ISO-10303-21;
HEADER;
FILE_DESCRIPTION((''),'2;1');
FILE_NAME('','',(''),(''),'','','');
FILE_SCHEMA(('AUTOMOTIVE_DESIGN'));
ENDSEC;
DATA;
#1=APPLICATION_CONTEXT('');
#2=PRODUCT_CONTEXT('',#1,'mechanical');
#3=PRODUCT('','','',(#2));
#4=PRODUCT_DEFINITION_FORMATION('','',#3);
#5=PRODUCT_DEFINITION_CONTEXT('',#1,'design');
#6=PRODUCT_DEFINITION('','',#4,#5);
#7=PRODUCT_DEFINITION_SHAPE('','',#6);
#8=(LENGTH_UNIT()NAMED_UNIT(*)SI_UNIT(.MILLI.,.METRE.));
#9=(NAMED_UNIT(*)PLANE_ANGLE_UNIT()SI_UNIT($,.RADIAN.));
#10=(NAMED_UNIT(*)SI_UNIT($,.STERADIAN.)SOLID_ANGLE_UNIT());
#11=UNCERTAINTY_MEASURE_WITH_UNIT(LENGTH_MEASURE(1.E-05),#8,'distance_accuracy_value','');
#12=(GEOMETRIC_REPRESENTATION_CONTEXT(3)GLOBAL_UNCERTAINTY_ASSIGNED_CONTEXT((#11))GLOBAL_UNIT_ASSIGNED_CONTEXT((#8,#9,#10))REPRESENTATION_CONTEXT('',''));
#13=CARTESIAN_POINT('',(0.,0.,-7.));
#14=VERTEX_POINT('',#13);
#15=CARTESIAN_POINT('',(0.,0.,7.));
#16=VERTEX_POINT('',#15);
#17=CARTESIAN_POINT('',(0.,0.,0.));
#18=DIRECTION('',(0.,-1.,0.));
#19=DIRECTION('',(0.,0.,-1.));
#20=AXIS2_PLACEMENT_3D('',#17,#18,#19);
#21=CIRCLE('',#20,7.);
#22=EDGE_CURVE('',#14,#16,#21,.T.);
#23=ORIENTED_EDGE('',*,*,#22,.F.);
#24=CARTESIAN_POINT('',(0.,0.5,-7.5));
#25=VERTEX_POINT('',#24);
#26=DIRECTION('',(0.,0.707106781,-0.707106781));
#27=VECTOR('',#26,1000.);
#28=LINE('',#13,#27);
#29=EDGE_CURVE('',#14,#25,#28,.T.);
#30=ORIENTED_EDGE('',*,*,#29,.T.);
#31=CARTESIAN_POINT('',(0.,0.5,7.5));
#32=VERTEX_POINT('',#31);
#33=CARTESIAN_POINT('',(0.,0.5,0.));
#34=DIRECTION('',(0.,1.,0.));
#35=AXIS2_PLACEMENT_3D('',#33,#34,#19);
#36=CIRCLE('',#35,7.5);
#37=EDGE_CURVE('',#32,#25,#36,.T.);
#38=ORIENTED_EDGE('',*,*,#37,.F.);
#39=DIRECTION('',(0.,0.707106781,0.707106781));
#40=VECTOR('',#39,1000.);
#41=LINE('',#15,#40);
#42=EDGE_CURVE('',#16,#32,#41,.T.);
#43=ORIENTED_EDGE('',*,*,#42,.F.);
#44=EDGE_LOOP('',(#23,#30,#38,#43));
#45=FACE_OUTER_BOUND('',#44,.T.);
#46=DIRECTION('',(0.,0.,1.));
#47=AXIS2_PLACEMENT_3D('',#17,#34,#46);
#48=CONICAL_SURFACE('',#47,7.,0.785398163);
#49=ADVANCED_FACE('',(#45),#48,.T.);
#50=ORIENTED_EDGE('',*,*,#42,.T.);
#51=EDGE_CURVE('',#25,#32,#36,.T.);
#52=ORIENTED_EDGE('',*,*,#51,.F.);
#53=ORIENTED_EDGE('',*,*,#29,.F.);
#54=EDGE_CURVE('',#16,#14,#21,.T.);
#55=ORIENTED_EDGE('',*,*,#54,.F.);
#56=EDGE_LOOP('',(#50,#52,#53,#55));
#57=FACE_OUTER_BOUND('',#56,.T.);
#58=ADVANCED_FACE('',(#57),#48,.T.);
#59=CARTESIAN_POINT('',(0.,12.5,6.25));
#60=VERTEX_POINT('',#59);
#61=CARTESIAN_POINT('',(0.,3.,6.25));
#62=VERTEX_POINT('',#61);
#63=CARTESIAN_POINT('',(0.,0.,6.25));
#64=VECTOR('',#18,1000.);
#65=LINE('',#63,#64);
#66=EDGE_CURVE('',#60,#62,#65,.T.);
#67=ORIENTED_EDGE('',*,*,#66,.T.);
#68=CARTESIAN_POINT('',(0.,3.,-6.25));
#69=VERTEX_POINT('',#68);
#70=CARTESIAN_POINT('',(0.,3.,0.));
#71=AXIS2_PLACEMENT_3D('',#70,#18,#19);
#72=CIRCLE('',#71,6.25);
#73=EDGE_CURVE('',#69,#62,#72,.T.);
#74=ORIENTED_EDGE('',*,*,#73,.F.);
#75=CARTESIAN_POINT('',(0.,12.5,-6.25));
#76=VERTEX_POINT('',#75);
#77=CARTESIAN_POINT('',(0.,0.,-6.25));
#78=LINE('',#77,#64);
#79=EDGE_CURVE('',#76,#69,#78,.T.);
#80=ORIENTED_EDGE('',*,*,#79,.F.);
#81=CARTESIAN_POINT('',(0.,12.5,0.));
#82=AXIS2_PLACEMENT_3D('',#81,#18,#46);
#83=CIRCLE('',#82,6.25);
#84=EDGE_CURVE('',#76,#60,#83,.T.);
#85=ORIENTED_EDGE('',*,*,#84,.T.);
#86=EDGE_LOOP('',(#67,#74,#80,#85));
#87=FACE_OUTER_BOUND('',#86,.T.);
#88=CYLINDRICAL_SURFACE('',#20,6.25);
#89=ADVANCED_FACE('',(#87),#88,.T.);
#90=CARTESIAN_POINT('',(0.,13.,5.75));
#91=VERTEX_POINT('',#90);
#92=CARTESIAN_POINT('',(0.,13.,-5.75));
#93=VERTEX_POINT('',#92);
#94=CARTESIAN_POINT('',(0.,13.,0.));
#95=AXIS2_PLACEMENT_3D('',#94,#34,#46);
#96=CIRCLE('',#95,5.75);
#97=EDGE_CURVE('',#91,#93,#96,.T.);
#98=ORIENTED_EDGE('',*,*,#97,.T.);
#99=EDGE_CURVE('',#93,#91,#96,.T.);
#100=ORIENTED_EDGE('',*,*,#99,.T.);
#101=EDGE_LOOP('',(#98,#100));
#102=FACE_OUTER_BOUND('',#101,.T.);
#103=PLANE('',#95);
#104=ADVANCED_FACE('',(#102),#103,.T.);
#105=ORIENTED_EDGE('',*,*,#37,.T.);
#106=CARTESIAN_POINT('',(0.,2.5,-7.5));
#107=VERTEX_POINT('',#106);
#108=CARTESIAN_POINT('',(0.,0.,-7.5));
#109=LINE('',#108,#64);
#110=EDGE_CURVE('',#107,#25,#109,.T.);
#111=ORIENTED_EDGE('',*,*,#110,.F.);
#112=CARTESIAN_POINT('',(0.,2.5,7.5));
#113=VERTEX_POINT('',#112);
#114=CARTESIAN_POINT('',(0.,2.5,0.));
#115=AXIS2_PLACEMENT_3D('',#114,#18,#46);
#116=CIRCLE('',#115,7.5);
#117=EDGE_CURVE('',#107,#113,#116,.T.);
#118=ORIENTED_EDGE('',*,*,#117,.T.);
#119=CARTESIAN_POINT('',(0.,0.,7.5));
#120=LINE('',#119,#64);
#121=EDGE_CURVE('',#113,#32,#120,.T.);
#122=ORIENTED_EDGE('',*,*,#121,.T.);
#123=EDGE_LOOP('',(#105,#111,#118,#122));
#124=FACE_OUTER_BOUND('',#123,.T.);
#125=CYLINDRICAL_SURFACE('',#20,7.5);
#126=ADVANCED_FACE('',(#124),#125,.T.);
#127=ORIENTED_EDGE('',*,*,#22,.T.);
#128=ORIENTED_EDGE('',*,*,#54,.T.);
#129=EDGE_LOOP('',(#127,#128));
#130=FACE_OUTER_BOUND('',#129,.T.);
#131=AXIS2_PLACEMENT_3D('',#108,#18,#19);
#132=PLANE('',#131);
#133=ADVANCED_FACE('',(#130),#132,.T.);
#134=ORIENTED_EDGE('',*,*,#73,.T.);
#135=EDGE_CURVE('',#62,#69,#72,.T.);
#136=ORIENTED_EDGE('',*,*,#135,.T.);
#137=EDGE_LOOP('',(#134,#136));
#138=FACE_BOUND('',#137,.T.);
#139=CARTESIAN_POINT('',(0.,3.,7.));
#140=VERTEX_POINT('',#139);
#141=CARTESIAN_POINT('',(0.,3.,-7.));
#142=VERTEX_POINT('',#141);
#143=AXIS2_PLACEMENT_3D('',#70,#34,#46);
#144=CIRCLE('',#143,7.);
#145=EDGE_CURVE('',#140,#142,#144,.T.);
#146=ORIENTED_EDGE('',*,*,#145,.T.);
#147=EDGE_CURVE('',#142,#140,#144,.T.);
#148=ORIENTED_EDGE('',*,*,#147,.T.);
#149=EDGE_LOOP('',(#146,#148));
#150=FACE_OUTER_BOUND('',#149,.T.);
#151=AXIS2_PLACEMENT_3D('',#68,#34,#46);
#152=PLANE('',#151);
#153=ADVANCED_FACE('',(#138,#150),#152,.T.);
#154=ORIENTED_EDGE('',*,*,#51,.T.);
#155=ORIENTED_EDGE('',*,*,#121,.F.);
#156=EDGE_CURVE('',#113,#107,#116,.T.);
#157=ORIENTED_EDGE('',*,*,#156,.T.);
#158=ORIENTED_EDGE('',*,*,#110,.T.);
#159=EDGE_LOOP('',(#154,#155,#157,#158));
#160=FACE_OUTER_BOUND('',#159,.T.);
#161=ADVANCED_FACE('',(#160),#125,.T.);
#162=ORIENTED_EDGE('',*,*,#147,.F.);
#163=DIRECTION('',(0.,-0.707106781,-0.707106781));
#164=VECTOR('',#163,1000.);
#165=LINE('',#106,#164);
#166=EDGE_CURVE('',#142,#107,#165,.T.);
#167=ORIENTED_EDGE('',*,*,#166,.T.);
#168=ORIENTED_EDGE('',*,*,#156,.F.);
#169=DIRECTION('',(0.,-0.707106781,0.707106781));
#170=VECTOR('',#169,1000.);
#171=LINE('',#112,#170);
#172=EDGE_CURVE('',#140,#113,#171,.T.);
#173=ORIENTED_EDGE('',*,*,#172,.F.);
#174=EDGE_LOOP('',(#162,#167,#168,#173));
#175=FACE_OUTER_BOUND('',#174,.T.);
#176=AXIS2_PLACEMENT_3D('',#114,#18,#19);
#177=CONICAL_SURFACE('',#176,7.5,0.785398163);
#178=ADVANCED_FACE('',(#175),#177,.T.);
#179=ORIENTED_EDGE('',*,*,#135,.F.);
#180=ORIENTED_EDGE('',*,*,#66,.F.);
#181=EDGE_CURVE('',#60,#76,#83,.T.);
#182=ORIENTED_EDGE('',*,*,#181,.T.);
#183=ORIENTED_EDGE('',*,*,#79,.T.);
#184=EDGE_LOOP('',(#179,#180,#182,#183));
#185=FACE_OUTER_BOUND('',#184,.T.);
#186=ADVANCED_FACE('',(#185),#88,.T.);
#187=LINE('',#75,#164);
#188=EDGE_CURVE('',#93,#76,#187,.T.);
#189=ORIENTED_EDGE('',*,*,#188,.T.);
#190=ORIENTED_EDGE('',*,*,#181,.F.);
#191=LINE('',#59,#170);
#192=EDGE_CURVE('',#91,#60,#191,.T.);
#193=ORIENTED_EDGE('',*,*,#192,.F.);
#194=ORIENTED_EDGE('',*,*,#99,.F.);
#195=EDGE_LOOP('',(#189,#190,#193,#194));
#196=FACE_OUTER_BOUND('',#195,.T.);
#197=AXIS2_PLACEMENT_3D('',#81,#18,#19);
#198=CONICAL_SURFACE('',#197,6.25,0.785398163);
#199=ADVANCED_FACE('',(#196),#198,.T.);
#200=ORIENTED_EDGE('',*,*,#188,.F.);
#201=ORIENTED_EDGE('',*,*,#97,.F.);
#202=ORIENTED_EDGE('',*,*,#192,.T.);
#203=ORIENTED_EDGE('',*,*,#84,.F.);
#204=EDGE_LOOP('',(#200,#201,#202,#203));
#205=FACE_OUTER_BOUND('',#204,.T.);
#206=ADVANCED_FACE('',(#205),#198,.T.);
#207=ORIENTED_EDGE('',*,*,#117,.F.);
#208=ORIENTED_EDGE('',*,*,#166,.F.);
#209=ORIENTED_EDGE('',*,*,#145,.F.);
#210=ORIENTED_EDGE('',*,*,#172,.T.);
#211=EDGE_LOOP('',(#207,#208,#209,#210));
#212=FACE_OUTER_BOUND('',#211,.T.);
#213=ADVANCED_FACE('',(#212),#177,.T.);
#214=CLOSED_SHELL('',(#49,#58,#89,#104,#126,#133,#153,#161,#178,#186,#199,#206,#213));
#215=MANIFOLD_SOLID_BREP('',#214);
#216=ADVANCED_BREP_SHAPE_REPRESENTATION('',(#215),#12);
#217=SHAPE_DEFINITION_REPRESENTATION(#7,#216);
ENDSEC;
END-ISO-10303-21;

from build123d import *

# Parameters (mm, degrees)
CHAMFER1_SIZE = 0.5


with BuildPart() as part:
    # Sketch1 → Revolve1 (revolve)
    with BuildSketch(Plane(origin=(0, 0, 0), x_dir=(0, 0, -1), z_dir=(1, 0, 0))):
        Polygon((0, 13), (6.25, 13), (6.25, 3), (7.5, 3), (7.5, 0), (0, 0), align=None)
    revolve(axis=Axis((0, 0, 0), (0, 1, 0)))

    # Chamfer1
    chamfer1_edges = [part.edges().sort_by_distance(p)[0] for p in [
        (0, 0, 7.5),
        (0, 3, 7.5),
        (0, 13, 6.25),
    ]]
    chamfer(chamfer1_edges, length=CHAMFER1_SIZE)


solid = part.part
